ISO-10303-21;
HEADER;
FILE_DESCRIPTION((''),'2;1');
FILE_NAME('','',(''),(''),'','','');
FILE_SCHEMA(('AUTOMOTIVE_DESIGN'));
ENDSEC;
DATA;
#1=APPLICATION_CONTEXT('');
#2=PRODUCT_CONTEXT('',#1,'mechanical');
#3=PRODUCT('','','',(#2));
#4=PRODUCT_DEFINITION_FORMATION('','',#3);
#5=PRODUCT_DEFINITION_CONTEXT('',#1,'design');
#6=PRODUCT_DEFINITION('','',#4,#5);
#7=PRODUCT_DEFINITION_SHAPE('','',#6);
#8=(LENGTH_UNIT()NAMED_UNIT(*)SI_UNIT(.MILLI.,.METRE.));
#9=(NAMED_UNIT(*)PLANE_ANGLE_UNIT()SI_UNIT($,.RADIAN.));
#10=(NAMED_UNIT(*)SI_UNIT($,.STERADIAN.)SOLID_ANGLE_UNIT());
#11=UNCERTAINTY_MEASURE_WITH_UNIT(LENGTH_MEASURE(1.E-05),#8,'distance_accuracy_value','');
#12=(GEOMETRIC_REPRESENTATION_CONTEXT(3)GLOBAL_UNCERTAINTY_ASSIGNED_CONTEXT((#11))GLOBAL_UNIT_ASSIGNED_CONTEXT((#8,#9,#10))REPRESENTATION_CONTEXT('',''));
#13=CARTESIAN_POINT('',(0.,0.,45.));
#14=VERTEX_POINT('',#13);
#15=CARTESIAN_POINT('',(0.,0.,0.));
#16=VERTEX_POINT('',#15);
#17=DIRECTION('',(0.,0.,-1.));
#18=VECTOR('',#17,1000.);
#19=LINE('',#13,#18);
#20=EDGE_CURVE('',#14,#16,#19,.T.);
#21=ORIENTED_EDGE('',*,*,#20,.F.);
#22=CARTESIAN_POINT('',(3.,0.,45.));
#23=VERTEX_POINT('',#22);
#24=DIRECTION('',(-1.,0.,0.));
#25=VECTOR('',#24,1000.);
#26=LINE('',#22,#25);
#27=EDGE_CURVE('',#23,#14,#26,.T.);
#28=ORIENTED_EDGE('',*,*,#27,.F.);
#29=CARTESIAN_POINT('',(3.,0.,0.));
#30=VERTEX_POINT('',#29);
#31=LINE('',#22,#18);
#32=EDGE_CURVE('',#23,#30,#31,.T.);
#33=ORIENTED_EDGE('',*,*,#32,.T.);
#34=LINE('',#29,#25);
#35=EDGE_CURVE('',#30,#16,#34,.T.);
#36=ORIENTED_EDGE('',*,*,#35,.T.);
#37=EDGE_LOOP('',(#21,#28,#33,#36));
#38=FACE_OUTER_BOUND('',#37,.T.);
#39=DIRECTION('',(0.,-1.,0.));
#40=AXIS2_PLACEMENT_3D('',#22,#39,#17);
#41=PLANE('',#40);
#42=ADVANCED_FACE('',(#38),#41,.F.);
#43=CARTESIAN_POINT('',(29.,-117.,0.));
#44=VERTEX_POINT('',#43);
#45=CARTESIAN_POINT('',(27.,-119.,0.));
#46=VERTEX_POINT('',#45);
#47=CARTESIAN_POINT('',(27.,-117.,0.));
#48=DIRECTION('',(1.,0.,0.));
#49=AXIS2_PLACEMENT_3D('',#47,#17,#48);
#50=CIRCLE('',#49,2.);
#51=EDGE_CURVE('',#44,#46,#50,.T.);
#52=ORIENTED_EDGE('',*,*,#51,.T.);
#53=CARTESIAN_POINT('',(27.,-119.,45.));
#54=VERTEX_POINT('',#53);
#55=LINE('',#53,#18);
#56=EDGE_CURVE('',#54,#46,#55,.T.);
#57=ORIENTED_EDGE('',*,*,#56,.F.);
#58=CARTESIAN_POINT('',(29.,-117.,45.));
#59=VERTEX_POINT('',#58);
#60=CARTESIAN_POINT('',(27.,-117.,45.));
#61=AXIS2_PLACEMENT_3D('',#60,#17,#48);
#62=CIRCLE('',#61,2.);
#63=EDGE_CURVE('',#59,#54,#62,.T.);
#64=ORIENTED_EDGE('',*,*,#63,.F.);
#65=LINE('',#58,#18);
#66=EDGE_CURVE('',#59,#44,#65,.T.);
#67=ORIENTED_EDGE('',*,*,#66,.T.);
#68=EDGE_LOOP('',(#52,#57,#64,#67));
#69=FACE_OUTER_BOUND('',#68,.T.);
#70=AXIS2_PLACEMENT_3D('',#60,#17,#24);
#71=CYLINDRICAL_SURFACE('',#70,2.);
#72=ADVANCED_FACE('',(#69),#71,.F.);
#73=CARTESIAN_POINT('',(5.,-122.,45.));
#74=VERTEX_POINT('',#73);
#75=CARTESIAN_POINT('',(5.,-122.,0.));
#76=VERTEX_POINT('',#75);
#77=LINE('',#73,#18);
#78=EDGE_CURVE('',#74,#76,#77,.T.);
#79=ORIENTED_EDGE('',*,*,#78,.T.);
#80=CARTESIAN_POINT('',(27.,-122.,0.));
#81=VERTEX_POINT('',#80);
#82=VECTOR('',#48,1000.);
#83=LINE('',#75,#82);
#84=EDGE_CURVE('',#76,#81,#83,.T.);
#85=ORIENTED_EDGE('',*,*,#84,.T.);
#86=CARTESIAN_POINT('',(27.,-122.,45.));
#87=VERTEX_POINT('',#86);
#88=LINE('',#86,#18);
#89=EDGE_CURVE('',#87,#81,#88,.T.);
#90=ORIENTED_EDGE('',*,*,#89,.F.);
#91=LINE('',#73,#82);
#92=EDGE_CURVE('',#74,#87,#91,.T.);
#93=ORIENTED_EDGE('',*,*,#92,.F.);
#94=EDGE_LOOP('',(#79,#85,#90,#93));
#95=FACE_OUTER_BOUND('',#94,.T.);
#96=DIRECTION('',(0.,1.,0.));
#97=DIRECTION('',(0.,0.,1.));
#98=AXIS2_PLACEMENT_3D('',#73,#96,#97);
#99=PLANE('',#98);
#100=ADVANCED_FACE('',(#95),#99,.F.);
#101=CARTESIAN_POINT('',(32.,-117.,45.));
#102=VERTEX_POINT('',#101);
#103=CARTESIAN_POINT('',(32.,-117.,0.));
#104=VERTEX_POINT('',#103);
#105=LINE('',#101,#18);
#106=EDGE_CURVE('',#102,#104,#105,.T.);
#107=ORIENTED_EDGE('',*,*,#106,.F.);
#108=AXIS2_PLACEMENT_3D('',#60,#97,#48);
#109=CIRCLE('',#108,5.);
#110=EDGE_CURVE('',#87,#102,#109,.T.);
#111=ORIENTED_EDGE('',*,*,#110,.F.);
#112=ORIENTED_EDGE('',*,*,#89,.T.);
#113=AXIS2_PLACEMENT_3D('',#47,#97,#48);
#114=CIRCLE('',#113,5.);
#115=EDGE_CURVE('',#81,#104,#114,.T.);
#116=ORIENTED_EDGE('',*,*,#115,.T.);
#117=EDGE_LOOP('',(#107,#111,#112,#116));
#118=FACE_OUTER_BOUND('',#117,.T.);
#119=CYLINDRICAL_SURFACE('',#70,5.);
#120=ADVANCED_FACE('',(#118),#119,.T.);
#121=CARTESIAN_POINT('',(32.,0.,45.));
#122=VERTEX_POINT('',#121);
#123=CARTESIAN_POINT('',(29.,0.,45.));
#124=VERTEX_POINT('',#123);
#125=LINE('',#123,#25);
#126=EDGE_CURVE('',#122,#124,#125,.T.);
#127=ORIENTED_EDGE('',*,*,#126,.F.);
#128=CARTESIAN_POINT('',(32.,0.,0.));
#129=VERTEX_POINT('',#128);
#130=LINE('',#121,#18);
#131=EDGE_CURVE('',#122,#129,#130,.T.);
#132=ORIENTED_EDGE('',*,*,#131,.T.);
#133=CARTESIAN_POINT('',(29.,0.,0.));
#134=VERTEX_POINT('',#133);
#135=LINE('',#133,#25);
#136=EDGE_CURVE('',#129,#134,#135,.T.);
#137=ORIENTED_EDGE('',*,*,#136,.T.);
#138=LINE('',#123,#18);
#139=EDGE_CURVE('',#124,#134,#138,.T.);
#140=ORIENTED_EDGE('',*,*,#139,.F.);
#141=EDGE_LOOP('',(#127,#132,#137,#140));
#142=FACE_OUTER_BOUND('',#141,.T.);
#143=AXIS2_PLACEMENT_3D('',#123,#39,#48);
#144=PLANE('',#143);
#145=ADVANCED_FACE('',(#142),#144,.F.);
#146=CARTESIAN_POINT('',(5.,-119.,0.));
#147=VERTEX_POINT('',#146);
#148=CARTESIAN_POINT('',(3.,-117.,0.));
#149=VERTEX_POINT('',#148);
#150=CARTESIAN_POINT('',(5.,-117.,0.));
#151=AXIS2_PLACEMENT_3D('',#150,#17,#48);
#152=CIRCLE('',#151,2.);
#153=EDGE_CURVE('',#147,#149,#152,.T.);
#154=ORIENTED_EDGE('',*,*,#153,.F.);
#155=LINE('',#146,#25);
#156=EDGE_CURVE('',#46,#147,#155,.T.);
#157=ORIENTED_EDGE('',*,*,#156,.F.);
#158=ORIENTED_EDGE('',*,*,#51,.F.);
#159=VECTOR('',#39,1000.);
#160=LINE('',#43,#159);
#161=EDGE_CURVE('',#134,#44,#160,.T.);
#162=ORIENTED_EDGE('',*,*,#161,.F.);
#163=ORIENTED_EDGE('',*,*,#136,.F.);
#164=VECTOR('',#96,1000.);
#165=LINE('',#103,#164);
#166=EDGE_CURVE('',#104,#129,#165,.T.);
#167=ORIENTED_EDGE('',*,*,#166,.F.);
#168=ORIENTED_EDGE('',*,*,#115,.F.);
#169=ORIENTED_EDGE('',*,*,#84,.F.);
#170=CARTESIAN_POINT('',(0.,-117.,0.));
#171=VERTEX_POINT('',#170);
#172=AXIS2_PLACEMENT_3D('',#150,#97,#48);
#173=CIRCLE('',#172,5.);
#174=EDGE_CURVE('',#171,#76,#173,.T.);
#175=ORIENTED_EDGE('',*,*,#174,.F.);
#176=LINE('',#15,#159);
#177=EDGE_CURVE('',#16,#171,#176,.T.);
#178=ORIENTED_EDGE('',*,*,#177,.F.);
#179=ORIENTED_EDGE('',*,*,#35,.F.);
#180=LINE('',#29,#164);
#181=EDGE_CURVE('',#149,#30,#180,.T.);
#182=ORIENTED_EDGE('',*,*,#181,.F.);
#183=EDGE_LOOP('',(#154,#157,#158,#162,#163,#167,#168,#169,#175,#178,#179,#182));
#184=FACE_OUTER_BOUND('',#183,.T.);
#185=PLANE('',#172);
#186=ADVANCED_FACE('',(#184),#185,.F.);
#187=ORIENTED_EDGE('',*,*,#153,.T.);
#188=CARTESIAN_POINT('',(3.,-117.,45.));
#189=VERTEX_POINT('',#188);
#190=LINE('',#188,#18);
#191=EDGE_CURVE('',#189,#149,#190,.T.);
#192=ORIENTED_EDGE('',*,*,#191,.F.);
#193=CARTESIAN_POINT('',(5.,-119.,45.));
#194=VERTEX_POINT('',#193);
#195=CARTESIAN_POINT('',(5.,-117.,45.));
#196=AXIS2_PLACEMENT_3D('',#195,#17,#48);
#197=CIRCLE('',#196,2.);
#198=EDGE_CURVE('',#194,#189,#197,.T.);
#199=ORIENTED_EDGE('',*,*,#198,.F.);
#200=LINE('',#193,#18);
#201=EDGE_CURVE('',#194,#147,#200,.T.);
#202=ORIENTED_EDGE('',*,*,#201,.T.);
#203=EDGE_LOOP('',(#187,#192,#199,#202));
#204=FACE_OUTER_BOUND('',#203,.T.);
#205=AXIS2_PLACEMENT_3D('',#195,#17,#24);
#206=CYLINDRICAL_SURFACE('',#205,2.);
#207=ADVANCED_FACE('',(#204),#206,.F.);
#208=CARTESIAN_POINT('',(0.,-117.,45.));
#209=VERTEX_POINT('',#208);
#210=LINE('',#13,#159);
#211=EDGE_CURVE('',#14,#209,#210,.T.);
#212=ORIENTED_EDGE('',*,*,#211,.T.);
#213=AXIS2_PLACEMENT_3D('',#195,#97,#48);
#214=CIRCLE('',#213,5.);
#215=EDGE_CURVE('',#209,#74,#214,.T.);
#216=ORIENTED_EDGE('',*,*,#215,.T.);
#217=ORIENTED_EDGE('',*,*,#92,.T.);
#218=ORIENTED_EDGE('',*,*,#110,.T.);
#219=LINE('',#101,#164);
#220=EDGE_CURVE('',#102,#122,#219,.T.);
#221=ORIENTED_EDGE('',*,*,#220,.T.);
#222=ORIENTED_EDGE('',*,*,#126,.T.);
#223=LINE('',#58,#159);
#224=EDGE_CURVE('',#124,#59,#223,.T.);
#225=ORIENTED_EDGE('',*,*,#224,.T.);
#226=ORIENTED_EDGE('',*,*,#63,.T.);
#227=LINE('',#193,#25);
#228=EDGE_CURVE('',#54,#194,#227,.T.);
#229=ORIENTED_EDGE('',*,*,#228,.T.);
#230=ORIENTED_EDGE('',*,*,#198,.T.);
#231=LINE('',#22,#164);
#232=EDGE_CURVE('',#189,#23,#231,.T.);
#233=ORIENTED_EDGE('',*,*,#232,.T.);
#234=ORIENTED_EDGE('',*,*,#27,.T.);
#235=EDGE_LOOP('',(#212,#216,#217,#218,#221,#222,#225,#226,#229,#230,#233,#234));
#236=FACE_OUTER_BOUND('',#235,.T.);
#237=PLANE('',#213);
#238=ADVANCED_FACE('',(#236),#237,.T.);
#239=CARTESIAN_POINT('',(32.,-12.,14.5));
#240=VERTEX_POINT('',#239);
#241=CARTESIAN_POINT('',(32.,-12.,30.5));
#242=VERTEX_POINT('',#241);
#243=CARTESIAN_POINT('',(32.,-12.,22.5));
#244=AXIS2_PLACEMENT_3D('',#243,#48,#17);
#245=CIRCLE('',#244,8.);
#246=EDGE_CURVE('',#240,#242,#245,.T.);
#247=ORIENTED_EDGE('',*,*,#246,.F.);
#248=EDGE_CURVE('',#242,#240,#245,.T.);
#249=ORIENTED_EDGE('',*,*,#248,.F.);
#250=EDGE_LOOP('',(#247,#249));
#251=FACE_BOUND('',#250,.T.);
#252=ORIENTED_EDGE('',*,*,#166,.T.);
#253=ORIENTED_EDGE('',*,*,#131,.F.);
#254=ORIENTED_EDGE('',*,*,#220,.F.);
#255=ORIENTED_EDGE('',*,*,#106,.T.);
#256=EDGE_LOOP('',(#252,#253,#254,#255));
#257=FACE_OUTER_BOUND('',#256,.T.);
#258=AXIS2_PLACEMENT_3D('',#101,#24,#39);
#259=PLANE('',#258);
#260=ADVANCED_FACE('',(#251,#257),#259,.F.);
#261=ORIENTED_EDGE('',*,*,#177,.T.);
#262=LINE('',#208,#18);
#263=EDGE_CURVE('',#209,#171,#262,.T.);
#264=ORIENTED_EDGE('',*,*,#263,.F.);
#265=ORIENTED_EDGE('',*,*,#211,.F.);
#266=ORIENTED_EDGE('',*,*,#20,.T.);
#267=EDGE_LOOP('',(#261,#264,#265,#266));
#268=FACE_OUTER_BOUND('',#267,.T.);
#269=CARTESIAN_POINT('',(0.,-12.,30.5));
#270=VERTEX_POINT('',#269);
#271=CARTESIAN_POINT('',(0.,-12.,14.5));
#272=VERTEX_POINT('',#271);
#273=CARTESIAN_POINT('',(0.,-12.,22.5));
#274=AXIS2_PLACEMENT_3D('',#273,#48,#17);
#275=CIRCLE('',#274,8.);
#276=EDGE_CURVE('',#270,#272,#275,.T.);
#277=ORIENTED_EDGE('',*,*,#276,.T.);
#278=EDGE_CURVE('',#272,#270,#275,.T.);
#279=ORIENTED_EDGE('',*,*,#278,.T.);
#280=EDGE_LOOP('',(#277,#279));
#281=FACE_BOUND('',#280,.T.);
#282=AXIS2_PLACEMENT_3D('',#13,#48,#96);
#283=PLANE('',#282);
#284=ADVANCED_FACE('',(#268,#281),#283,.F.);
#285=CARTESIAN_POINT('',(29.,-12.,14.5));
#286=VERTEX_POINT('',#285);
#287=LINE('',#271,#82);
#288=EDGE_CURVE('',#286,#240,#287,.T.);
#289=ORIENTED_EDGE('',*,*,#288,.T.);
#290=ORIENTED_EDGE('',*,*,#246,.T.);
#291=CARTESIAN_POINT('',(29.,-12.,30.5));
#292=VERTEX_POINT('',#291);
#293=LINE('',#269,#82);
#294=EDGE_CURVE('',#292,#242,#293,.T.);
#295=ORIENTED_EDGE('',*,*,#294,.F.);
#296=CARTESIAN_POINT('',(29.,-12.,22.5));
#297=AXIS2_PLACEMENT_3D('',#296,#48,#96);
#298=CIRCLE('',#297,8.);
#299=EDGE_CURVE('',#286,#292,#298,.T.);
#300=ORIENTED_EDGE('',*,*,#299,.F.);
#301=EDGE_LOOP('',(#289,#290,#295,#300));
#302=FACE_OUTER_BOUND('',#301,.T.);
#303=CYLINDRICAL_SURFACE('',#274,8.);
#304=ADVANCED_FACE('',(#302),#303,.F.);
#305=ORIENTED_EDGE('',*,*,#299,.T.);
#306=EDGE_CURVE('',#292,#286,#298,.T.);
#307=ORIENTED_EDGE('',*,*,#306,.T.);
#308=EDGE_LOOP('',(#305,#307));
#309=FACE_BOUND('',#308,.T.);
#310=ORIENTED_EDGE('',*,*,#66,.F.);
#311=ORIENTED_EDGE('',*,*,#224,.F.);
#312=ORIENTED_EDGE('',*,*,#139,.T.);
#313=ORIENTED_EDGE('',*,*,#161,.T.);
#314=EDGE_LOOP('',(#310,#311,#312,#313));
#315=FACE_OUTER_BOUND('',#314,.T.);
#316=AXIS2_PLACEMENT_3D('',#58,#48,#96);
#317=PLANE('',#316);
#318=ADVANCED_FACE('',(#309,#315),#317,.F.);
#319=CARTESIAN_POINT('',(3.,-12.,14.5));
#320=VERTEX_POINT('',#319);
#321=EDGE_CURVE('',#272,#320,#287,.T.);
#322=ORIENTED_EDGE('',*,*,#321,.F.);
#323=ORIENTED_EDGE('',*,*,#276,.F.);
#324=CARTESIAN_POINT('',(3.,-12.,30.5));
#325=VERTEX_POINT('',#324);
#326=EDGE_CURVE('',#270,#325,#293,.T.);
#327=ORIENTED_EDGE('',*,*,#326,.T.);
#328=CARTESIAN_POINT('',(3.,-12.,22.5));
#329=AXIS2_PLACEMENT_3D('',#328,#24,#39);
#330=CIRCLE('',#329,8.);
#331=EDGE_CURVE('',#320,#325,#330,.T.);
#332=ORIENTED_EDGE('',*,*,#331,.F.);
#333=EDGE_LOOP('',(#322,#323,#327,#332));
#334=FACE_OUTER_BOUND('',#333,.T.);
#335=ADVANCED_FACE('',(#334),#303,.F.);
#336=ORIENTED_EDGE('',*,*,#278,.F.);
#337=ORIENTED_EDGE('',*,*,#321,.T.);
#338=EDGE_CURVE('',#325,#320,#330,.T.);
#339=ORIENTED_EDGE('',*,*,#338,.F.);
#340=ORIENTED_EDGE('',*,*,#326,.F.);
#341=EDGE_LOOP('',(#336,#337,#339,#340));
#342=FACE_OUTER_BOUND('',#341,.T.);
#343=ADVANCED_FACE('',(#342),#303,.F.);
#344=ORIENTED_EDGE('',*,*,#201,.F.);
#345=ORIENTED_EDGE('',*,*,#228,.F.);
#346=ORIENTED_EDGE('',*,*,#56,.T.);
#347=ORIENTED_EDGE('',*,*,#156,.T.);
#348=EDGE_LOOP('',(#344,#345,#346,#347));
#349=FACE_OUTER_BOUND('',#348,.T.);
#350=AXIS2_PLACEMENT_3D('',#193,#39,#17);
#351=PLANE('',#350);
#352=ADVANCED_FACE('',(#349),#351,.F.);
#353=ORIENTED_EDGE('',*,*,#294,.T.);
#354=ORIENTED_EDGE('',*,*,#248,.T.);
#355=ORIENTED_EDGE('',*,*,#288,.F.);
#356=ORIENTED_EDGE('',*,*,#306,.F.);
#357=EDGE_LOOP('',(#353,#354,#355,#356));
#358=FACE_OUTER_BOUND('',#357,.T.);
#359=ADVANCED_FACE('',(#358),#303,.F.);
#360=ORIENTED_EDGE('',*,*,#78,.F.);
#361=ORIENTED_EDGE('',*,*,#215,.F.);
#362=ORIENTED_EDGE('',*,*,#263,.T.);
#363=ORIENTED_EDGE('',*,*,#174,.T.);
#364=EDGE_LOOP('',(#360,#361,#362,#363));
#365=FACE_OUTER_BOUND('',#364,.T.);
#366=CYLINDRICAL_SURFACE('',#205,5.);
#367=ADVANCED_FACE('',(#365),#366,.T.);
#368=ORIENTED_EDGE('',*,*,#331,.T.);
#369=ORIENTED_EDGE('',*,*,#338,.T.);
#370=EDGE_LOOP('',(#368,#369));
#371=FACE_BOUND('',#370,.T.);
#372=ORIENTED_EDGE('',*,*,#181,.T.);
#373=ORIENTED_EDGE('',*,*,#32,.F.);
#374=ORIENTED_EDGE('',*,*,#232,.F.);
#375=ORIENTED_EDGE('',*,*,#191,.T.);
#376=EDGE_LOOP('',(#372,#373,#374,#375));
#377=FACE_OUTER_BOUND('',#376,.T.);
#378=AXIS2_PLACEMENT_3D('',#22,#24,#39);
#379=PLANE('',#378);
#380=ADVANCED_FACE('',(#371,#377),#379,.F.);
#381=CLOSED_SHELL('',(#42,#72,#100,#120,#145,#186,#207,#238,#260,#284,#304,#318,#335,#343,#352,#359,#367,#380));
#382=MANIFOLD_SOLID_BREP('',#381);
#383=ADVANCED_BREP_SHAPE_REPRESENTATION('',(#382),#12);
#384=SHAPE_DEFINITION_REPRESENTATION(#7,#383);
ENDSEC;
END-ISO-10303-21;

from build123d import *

# Parameters (mm, degrees)
BOSS_EXTRUDE1_DEPTH = 45
SKETCH2_R           = 8
CUT_EXTRUDE1_DEPTH  = 134.914151605


with BuildPart() as part:
    # Sketch1 → Boss-Extrude1 (new body)
    with BuildSketch(Plane.XY):
        with BuildLine():
            Line((0, 0), (0, -117))
            ThreePointArc((0, -117), (1.464466094, -120.535533906), (5, -122))
            Line((5, -122), (27, -122))
            ThreePointArc((27, -122), (30.535533906, -120.535533906), (32, -117))
            Line((32, -117), (32, 0))
            Line((32, 0), (29, 0))
            Line((29, 0), (29, -117))
            ThreePointArc((29, -117), (28.414213562, -118.414213562), (27, -119))
            Line((27, -119), (5, -119))
            ThreePointArc((5, -119), (3.585786438, -118.414213562), (3, -117))
            Line((3, -117), (3, 0))
            Line((3, 0), (0, 0))
        make_face()
    extrude(amount=BOSS_EXTRUDE1_DEPTH)

    # Sketch2 → Cut-Extrude1 (cut, through all)
    with BuildSketch(Plane(origin=(32, 0, 0), x_dir=(0, 0, -1), z_dir=(1, 0, 0))):
        with Locations((-22.5, -12)):
            Circle(SKETCH2_R)
    extrude(amount=-CUT_EXTRUDE1_DEPTH, mode=Mode.SUBTRACT)


solid = part.part
